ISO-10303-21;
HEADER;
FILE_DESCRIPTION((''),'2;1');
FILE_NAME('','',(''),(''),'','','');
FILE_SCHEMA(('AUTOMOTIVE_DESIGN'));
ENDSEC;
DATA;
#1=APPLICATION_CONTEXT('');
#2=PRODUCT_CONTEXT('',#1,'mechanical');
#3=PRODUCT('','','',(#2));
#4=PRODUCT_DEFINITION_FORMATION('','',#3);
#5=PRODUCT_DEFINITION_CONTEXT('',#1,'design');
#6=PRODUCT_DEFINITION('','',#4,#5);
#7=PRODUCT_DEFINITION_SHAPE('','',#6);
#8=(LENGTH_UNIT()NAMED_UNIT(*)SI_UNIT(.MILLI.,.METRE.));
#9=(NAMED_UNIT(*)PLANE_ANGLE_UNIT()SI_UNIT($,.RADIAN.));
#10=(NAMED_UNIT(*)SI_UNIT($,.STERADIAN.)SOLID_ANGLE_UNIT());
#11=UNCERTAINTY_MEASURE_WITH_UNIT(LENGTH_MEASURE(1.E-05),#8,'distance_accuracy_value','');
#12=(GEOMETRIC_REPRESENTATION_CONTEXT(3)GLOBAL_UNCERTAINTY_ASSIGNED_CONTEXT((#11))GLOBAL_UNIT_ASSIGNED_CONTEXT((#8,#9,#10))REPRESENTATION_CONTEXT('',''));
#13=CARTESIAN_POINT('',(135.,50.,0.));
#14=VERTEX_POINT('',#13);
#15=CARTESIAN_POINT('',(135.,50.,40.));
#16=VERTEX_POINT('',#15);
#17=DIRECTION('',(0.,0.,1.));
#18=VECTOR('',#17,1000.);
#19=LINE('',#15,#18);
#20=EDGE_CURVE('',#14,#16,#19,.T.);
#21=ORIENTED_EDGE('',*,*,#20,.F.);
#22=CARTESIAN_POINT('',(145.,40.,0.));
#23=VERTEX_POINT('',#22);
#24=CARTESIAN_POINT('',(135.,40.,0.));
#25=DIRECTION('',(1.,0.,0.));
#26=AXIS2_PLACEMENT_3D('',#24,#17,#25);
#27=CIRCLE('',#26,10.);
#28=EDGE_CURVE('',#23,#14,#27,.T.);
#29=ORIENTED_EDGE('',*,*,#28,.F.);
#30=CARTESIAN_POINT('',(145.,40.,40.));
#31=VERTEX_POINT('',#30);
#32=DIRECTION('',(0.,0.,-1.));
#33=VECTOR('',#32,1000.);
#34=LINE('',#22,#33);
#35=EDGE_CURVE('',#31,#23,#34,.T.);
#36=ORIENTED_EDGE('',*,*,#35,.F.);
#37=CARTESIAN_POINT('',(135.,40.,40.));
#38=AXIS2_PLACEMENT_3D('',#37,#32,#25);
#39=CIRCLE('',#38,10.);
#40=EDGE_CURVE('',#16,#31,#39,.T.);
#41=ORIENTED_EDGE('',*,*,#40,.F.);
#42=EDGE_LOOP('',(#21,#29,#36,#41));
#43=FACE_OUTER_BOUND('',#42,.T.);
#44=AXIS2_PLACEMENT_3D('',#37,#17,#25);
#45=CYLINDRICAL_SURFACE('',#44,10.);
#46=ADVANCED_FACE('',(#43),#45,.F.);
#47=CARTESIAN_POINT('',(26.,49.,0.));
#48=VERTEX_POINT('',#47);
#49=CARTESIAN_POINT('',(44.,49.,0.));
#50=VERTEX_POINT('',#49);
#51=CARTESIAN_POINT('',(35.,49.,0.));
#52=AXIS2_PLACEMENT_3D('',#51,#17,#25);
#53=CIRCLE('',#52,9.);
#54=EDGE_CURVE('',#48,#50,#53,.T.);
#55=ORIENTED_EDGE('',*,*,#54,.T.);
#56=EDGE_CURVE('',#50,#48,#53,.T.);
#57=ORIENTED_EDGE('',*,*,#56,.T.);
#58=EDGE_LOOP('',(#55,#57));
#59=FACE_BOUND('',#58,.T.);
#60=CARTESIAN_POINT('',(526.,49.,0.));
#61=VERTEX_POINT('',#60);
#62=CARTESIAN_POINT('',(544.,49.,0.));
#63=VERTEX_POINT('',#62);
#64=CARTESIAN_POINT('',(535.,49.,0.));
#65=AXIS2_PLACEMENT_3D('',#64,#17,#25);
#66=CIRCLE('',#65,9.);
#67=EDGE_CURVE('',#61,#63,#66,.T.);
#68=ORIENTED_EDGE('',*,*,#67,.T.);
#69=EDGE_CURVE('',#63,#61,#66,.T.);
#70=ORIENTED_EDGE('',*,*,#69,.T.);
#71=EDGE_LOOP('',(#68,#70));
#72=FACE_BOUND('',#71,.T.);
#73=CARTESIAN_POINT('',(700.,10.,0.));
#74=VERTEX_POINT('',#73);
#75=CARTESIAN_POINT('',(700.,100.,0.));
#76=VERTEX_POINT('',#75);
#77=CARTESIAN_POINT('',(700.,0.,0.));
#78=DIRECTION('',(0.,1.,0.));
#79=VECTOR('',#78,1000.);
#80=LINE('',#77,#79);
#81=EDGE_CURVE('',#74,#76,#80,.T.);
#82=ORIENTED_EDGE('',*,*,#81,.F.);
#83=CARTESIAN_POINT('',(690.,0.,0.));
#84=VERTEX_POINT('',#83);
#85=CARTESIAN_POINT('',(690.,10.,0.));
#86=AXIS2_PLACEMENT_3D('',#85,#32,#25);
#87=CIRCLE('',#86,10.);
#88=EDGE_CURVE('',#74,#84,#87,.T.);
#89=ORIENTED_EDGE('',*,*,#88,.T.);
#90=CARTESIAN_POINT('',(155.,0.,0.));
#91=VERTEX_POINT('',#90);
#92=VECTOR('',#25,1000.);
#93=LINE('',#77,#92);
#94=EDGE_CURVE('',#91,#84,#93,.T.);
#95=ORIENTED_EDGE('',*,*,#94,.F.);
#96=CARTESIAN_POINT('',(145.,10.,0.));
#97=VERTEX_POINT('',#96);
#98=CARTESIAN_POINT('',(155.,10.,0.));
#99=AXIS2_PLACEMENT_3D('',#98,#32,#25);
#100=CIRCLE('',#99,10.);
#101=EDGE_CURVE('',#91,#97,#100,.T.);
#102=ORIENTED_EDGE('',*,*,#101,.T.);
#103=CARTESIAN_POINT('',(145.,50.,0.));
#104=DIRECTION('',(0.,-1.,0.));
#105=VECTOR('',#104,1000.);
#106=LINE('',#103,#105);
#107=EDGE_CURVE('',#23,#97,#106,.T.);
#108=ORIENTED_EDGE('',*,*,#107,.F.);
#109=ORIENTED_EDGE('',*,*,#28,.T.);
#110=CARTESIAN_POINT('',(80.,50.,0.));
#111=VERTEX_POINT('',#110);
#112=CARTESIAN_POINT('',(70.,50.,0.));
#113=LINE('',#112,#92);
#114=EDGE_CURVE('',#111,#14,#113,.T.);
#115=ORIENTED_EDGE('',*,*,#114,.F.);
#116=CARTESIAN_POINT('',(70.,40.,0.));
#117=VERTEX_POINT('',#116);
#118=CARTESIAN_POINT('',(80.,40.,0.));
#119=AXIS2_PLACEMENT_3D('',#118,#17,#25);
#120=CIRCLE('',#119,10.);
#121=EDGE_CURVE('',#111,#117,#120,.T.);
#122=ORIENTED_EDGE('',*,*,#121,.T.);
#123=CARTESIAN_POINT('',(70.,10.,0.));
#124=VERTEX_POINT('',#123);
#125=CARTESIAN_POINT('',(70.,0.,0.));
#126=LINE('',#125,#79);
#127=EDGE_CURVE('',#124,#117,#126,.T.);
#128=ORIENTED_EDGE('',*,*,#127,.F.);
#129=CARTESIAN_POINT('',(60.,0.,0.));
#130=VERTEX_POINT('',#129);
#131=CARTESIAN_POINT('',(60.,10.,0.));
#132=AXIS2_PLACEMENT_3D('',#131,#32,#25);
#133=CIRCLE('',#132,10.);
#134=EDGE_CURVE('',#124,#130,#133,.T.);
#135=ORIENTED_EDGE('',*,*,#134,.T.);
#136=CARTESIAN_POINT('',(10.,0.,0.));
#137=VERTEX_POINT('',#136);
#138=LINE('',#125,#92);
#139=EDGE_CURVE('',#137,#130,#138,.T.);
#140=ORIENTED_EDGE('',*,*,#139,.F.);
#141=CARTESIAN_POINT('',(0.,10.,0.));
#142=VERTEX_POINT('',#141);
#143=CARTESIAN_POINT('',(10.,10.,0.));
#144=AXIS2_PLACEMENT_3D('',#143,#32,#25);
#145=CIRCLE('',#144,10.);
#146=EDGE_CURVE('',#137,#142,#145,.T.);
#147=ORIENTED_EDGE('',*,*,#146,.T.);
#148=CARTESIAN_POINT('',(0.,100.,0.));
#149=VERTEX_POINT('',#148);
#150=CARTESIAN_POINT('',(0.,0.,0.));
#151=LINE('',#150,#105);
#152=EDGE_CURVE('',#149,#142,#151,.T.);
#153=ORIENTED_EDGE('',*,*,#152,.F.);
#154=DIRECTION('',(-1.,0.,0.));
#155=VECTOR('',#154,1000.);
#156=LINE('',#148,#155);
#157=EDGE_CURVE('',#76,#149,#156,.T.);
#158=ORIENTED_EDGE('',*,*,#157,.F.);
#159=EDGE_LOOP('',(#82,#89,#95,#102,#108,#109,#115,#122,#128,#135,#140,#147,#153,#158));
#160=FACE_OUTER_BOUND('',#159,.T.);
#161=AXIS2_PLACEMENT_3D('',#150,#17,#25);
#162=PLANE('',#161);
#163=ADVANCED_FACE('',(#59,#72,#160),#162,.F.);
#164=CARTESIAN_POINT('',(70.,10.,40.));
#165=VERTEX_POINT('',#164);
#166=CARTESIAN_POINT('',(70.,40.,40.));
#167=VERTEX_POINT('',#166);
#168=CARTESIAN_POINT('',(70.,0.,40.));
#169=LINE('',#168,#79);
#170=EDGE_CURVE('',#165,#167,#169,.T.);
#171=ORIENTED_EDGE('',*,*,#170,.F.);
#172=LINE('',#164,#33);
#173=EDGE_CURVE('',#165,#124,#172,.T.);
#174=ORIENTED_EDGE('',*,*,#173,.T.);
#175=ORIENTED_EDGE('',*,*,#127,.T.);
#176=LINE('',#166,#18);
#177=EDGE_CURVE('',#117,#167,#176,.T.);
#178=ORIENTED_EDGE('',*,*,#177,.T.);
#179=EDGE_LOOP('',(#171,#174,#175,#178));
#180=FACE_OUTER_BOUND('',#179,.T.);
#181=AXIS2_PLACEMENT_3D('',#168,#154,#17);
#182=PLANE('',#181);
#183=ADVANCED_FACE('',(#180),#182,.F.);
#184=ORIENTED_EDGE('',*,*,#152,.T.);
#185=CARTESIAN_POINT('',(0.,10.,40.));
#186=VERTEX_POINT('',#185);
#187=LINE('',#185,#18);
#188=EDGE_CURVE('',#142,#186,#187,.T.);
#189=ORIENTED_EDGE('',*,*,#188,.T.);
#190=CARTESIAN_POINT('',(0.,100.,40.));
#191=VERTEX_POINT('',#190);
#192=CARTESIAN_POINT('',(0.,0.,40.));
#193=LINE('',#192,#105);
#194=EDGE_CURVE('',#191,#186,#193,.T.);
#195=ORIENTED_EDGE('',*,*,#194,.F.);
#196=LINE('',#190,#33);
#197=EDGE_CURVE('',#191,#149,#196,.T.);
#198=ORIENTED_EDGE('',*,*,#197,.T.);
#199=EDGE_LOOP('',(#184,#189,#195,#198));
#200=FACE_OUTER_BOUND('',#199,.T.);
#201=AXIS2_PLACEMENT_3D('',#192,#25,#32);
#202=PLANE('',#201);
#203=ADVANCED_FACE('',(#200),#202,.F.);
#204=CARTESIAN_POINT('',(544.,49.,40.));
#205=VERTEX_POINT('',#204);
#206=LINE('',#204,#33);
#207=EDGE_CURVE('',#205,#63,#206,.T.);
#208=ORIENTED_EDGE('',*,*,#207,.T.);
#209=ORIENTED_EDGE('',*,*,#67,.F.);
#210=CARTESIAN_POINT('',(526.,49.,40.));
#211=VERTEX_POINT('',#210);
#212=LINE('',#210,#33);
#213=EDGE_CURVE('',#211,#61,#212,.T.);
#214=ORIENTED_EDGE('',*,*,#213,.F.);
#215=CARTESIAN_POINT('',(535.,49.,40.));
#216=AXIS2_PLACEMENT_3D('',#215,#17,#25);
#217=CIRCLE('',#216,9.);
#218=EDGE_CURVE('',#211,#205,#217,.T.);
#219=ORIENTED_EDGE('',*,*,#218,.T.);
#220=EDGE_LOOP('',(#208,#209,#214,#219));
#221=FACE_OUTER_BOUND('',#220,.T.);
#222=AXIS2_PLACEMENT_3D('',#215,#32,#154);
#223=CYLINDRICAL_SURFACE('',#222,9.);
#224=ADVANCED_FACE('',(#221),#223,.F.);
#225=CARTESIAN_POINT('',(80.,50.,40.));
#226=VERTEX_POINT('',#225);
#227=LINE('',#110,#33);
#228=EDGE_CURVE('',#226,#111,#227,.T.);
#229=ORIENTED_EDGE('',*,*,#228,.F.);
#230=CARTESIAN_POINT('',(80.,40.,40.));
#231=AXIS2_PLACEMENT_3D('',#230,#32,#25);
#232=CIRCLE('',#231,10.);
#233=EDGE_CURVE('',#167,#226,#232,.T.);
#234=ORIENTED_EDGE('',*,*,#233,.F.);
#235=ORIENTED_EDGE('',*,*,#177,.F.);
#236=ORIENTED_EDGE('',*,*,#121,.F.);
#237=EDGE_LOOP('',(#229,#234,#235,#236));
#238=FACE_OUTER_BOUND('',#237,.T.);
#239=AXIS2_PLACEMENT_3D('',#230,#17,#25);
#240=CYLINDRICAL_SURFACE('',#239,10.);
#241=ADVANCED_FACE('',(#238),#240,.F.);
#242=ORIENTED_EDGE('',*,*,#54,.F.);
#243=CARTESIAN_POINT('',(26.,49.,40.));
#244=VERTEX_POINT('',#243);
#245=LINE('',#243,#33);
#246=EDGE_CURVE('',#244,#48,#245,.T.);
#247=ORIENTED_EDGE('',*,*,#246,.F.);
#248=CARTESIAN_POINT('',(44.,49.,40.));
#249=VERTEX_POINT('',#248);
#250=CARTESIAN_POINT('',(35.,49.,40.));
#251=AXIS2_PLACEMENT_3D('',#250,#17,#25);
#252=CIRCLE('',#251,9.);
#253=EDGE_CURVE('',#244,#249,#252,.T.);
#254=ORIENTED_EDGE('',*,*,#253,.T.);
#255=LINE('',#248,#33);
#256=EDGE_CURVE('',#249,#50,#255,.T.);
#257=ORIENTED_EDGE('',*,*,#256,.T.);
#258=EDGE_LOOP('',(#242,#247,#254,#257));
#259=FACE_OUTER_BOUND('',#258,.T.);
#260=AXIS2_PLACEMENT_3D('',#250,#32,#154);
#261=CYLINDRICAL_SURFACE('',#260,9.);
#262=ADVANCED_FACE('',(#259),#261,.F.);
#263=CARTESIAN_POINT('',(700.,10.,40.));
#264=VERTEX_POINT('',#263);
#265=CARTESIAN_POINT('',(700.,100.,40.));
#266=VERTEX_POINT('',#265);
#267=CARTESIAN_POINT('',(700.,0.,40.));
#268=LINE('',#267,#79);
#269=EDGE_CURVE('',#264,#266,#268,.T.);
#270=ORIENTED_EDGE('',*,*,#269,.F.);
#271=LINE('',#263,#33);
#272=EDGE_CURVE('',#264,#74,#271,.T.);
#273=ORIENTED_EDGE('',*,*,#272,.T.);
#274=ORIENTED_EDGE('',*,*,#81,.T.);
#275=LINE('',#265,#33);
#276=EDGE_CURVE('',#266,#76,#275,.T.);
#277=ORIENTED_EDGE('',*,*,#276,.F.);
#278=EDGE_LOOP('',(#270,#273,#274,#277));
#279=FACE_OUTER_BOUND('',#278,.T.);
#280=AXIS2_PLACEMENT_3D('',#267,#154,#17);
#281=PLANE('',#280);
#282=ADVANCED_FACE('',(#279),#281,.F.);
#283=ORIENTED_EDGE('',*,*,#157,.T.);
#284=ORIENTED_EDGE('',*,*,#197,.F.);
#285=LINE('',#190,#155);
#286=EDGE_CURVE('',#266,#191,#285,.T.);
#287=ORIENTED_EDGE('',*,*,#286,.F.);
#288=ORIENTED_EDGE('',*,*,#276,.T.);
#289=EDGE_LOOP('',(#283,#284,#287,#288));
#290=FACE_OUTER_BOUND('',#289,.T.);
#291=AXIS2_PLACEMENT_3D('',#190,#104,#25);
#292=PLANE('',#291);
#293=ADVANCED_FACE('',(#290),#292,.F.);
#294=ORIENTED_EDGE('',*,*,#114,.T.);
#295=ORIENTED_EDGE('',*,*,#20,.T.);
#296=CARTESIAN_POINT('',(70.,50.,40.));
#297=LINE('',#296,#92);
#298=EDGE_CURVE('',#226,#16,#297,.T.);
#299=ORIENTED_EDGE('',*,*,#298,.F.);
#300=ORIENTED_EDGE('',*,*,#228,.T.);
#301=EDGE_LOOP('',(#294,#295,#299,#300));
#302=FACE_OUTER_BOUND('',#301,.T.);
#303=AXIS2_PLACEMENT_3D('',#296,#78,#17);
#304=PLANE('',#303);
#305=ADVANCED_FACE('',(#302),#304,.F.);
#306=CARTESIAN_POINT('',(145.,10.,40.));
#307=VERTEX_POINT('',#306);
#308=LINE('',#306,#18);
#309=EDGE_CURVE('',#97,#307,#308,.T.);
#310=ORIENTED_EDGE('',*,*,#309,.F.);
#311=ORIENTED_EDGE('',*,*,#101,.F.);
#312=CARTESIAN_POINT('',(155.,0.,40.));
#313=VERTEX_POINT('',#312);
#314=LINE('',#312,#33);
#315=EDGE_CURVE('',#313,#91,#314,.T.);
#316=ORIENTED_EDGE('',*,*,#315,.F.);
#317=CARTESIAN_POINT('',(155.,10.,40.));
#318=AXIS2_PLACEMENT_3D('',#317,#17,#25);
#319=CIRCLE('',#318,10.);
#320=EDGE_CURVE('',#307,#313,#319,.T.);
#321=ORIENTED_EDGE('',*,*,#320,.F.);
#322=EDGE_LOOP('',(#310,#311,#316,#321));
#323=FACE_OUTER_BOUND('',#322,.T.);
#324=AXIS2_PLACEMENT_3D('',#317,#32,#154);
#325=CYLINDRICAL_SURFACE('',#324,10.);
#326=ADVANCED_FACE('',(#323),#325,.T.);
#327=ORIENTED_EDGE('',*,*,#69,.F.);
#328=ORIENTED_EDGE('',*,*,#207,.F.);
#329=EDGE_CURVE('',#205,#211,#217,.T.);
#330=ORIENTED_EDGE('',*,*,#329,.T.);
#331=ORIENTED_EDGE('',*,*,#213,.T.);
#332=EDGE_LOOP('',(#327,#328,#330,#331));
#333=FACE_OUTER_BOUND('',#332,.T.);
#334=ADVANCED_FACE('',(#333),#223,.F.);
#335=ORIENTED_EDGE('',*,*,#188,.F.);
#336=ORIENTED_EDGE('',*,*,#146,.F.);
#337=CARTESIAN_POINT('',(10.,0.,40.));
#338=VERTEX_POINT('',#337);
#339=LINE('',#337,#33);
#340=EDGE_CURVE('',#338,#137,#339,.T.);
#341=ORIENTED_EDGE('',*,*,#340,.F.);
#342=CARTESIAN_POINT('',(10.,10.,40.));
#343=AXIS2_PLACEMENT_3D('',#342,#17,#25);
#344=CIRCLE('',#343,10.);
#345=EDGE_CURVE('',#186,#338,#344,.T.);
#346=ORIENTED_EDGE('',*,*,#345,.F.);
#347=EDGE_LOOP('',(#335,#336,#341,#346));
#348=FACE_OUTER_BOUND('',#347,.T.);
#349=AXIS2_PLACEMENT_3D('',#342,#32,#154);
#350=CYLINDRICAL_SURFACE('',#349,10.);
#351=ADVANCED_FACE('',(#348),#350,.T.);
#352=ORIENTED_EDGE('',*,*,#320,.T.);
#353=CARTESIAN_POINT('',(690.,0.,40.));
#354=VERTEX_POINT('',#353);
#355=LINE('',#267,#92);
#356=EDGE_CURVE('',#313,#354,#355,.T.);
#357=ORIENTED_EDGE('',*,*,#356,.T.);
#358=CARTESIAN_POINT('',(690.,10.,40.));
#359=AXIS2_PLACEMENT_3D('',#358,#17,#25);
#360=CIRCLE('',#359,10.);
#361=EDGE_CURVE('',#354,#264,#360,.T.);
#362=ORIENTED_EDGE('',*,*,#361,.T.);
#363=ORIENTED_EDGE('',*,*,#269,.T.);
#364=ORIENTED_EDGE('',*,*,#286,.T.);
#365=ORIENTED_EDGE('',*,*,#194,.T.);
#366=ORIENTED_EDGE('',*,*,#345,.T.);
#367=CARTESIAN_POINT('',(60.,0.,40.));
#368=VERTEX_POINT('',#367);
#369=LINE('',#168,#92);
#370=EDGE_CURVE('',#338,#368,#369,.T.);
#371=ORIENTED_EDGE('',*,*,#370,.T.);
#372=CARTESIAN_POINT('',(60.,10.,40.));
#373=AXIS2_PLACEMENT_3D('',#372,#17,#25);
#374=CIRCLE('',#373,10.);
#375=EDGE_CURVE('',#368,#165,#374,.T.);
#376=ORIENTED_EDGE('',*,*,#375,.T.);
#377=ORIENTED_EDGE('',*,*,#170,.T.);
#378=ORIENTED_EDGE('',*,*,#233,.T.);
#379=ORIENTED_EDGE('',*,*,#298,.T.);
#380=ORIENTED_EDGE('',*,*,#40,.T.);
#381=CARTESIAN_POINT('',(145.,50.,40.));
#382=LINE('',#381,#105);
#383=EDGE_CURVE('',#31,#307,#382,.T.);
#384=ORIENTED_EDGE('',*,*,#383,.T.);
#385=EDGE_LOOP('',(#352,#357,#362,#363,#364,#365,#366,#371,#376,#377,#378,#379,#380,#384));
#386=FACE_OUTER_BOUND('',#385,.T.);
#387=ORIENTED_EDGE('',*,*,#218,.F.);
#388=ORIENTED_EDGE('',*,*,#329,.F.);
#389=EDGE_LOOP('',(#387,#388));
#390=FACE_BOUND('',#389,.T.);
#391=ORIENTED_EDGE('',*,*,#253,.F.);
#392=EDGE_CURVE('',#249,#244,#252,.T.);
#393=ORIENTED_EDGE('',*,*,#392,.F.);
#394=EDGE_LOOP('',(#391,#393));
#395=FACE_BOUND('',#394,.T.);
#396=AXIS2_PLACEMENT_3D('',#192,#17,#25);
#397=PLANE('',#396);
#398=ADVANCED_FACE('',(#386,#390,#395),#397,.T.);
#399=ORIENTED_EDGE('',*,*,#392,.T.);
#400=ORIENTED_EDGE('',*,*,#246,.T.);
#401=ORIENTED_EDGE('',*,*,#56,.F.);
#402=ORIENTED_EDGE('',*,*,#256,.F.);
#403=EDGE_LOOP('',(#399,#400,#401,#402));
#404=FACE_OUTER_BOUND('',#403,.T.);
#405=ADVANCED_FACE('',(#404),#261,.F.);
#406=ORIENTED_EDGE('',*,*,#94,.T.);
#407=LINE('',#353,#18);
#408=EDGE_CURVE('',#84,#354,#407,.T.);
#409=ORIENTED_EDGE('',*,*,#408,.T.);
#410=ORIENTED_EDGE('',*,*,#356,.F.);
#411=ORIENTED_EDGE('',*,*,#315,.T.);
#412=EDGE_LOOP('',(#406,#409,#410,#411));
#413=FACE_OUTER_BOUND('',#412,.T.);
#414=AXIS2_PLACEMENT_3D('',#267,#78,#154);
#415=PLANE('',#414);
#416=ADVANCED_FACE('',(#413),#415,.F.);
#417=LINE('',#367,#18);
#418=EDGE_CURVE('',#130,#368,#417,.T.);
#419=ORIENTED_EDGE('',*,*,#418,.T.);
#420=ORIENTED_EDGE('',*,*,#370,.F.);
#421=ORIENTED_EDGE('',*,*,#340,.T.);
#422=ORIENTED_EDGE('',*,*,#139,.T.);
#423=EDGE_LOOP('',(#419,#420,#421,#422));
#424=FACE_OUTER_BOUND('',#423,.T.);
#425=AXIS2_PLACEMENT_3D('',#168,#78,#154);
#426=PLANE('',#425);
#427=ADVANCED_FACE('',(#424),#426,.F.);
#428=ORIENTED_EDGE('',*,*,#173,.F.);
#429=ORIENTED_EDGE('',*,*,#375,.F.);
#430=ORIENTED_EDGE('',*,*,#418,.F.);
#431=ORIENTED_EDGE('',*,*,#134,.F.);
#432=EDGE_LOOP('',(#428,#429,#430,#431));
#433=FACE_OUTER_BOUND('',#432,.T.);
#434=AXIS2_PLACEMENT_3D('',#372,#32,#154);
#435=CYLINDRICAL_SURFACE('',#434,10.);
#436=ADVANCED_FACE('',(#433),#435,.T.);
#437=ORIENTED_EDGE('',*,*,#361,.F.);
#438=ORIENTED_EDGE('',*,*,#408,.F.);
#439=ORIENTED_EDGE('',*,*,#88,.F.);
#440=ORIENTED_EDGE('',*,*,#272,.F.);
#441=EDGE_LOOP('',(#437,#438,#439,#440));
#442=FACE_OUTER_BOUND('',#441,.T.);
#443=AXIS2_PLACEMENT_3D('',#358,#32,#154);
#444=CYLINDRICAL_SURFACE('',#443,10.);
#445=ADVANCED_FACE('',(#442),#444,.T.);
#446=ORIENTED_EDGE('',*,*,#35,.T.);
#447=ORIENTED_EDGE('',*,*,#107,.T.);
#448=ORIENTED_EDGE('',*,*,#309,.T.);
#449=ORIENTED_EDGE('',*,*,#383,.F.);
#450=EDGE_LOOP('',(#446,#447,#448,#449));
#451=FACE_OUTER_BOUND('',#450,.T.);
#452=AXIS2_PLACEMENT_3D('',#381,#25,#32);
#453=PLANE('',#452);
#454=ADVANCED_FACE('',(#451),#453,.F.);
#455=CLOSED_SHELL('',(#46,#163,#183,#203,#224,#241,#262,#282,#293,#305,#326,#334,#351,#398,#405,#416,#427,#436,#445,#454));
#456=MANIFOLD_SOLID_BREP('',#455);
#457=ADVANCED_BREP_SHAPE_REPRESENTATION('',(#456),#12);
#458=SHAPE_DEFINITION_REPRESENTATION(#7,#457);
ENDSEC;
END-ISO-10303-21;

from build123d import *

# Parameters (mm, degrees)
SKETCH1_R           = 9
BOSS_EXTRUDE1_DEPTH = 40
FILLET1_R           = 10


with BuildPart() as part:
    # Sketch1 → Boss-Extrude1 (new body)
    with BuildSketch(Plane.XY):
        Polygon((70, 0), (70, 50), (145, 50), (145, 0), (700, 0), (700, 100), (0, 100), (0, 0), align=None)
        with Locations((35, 49)):
            Circle(SKETCH1_R, mode=Mode.SUBTRACT)
        with Locations((535, 49)):
            Circle(SKETCH1_R, mode=Mode.SUBTRACT)
    extrude(amount=BOSS_EXTRUDE1_DEPTH)

    # Fillet1
    fillet1_edges = [part.edges().sort_by_distance(p)[0] for p in [
        (145, 0, 20),
        (145, 50, 20),
        (70, 50, 20),
        (70, 0, 20),
        (0, 0, 20),
        (700, 0, 20),
    ]]
    fillet(fillet1_edges, radius=FILLET1_R)


solid = part.part
